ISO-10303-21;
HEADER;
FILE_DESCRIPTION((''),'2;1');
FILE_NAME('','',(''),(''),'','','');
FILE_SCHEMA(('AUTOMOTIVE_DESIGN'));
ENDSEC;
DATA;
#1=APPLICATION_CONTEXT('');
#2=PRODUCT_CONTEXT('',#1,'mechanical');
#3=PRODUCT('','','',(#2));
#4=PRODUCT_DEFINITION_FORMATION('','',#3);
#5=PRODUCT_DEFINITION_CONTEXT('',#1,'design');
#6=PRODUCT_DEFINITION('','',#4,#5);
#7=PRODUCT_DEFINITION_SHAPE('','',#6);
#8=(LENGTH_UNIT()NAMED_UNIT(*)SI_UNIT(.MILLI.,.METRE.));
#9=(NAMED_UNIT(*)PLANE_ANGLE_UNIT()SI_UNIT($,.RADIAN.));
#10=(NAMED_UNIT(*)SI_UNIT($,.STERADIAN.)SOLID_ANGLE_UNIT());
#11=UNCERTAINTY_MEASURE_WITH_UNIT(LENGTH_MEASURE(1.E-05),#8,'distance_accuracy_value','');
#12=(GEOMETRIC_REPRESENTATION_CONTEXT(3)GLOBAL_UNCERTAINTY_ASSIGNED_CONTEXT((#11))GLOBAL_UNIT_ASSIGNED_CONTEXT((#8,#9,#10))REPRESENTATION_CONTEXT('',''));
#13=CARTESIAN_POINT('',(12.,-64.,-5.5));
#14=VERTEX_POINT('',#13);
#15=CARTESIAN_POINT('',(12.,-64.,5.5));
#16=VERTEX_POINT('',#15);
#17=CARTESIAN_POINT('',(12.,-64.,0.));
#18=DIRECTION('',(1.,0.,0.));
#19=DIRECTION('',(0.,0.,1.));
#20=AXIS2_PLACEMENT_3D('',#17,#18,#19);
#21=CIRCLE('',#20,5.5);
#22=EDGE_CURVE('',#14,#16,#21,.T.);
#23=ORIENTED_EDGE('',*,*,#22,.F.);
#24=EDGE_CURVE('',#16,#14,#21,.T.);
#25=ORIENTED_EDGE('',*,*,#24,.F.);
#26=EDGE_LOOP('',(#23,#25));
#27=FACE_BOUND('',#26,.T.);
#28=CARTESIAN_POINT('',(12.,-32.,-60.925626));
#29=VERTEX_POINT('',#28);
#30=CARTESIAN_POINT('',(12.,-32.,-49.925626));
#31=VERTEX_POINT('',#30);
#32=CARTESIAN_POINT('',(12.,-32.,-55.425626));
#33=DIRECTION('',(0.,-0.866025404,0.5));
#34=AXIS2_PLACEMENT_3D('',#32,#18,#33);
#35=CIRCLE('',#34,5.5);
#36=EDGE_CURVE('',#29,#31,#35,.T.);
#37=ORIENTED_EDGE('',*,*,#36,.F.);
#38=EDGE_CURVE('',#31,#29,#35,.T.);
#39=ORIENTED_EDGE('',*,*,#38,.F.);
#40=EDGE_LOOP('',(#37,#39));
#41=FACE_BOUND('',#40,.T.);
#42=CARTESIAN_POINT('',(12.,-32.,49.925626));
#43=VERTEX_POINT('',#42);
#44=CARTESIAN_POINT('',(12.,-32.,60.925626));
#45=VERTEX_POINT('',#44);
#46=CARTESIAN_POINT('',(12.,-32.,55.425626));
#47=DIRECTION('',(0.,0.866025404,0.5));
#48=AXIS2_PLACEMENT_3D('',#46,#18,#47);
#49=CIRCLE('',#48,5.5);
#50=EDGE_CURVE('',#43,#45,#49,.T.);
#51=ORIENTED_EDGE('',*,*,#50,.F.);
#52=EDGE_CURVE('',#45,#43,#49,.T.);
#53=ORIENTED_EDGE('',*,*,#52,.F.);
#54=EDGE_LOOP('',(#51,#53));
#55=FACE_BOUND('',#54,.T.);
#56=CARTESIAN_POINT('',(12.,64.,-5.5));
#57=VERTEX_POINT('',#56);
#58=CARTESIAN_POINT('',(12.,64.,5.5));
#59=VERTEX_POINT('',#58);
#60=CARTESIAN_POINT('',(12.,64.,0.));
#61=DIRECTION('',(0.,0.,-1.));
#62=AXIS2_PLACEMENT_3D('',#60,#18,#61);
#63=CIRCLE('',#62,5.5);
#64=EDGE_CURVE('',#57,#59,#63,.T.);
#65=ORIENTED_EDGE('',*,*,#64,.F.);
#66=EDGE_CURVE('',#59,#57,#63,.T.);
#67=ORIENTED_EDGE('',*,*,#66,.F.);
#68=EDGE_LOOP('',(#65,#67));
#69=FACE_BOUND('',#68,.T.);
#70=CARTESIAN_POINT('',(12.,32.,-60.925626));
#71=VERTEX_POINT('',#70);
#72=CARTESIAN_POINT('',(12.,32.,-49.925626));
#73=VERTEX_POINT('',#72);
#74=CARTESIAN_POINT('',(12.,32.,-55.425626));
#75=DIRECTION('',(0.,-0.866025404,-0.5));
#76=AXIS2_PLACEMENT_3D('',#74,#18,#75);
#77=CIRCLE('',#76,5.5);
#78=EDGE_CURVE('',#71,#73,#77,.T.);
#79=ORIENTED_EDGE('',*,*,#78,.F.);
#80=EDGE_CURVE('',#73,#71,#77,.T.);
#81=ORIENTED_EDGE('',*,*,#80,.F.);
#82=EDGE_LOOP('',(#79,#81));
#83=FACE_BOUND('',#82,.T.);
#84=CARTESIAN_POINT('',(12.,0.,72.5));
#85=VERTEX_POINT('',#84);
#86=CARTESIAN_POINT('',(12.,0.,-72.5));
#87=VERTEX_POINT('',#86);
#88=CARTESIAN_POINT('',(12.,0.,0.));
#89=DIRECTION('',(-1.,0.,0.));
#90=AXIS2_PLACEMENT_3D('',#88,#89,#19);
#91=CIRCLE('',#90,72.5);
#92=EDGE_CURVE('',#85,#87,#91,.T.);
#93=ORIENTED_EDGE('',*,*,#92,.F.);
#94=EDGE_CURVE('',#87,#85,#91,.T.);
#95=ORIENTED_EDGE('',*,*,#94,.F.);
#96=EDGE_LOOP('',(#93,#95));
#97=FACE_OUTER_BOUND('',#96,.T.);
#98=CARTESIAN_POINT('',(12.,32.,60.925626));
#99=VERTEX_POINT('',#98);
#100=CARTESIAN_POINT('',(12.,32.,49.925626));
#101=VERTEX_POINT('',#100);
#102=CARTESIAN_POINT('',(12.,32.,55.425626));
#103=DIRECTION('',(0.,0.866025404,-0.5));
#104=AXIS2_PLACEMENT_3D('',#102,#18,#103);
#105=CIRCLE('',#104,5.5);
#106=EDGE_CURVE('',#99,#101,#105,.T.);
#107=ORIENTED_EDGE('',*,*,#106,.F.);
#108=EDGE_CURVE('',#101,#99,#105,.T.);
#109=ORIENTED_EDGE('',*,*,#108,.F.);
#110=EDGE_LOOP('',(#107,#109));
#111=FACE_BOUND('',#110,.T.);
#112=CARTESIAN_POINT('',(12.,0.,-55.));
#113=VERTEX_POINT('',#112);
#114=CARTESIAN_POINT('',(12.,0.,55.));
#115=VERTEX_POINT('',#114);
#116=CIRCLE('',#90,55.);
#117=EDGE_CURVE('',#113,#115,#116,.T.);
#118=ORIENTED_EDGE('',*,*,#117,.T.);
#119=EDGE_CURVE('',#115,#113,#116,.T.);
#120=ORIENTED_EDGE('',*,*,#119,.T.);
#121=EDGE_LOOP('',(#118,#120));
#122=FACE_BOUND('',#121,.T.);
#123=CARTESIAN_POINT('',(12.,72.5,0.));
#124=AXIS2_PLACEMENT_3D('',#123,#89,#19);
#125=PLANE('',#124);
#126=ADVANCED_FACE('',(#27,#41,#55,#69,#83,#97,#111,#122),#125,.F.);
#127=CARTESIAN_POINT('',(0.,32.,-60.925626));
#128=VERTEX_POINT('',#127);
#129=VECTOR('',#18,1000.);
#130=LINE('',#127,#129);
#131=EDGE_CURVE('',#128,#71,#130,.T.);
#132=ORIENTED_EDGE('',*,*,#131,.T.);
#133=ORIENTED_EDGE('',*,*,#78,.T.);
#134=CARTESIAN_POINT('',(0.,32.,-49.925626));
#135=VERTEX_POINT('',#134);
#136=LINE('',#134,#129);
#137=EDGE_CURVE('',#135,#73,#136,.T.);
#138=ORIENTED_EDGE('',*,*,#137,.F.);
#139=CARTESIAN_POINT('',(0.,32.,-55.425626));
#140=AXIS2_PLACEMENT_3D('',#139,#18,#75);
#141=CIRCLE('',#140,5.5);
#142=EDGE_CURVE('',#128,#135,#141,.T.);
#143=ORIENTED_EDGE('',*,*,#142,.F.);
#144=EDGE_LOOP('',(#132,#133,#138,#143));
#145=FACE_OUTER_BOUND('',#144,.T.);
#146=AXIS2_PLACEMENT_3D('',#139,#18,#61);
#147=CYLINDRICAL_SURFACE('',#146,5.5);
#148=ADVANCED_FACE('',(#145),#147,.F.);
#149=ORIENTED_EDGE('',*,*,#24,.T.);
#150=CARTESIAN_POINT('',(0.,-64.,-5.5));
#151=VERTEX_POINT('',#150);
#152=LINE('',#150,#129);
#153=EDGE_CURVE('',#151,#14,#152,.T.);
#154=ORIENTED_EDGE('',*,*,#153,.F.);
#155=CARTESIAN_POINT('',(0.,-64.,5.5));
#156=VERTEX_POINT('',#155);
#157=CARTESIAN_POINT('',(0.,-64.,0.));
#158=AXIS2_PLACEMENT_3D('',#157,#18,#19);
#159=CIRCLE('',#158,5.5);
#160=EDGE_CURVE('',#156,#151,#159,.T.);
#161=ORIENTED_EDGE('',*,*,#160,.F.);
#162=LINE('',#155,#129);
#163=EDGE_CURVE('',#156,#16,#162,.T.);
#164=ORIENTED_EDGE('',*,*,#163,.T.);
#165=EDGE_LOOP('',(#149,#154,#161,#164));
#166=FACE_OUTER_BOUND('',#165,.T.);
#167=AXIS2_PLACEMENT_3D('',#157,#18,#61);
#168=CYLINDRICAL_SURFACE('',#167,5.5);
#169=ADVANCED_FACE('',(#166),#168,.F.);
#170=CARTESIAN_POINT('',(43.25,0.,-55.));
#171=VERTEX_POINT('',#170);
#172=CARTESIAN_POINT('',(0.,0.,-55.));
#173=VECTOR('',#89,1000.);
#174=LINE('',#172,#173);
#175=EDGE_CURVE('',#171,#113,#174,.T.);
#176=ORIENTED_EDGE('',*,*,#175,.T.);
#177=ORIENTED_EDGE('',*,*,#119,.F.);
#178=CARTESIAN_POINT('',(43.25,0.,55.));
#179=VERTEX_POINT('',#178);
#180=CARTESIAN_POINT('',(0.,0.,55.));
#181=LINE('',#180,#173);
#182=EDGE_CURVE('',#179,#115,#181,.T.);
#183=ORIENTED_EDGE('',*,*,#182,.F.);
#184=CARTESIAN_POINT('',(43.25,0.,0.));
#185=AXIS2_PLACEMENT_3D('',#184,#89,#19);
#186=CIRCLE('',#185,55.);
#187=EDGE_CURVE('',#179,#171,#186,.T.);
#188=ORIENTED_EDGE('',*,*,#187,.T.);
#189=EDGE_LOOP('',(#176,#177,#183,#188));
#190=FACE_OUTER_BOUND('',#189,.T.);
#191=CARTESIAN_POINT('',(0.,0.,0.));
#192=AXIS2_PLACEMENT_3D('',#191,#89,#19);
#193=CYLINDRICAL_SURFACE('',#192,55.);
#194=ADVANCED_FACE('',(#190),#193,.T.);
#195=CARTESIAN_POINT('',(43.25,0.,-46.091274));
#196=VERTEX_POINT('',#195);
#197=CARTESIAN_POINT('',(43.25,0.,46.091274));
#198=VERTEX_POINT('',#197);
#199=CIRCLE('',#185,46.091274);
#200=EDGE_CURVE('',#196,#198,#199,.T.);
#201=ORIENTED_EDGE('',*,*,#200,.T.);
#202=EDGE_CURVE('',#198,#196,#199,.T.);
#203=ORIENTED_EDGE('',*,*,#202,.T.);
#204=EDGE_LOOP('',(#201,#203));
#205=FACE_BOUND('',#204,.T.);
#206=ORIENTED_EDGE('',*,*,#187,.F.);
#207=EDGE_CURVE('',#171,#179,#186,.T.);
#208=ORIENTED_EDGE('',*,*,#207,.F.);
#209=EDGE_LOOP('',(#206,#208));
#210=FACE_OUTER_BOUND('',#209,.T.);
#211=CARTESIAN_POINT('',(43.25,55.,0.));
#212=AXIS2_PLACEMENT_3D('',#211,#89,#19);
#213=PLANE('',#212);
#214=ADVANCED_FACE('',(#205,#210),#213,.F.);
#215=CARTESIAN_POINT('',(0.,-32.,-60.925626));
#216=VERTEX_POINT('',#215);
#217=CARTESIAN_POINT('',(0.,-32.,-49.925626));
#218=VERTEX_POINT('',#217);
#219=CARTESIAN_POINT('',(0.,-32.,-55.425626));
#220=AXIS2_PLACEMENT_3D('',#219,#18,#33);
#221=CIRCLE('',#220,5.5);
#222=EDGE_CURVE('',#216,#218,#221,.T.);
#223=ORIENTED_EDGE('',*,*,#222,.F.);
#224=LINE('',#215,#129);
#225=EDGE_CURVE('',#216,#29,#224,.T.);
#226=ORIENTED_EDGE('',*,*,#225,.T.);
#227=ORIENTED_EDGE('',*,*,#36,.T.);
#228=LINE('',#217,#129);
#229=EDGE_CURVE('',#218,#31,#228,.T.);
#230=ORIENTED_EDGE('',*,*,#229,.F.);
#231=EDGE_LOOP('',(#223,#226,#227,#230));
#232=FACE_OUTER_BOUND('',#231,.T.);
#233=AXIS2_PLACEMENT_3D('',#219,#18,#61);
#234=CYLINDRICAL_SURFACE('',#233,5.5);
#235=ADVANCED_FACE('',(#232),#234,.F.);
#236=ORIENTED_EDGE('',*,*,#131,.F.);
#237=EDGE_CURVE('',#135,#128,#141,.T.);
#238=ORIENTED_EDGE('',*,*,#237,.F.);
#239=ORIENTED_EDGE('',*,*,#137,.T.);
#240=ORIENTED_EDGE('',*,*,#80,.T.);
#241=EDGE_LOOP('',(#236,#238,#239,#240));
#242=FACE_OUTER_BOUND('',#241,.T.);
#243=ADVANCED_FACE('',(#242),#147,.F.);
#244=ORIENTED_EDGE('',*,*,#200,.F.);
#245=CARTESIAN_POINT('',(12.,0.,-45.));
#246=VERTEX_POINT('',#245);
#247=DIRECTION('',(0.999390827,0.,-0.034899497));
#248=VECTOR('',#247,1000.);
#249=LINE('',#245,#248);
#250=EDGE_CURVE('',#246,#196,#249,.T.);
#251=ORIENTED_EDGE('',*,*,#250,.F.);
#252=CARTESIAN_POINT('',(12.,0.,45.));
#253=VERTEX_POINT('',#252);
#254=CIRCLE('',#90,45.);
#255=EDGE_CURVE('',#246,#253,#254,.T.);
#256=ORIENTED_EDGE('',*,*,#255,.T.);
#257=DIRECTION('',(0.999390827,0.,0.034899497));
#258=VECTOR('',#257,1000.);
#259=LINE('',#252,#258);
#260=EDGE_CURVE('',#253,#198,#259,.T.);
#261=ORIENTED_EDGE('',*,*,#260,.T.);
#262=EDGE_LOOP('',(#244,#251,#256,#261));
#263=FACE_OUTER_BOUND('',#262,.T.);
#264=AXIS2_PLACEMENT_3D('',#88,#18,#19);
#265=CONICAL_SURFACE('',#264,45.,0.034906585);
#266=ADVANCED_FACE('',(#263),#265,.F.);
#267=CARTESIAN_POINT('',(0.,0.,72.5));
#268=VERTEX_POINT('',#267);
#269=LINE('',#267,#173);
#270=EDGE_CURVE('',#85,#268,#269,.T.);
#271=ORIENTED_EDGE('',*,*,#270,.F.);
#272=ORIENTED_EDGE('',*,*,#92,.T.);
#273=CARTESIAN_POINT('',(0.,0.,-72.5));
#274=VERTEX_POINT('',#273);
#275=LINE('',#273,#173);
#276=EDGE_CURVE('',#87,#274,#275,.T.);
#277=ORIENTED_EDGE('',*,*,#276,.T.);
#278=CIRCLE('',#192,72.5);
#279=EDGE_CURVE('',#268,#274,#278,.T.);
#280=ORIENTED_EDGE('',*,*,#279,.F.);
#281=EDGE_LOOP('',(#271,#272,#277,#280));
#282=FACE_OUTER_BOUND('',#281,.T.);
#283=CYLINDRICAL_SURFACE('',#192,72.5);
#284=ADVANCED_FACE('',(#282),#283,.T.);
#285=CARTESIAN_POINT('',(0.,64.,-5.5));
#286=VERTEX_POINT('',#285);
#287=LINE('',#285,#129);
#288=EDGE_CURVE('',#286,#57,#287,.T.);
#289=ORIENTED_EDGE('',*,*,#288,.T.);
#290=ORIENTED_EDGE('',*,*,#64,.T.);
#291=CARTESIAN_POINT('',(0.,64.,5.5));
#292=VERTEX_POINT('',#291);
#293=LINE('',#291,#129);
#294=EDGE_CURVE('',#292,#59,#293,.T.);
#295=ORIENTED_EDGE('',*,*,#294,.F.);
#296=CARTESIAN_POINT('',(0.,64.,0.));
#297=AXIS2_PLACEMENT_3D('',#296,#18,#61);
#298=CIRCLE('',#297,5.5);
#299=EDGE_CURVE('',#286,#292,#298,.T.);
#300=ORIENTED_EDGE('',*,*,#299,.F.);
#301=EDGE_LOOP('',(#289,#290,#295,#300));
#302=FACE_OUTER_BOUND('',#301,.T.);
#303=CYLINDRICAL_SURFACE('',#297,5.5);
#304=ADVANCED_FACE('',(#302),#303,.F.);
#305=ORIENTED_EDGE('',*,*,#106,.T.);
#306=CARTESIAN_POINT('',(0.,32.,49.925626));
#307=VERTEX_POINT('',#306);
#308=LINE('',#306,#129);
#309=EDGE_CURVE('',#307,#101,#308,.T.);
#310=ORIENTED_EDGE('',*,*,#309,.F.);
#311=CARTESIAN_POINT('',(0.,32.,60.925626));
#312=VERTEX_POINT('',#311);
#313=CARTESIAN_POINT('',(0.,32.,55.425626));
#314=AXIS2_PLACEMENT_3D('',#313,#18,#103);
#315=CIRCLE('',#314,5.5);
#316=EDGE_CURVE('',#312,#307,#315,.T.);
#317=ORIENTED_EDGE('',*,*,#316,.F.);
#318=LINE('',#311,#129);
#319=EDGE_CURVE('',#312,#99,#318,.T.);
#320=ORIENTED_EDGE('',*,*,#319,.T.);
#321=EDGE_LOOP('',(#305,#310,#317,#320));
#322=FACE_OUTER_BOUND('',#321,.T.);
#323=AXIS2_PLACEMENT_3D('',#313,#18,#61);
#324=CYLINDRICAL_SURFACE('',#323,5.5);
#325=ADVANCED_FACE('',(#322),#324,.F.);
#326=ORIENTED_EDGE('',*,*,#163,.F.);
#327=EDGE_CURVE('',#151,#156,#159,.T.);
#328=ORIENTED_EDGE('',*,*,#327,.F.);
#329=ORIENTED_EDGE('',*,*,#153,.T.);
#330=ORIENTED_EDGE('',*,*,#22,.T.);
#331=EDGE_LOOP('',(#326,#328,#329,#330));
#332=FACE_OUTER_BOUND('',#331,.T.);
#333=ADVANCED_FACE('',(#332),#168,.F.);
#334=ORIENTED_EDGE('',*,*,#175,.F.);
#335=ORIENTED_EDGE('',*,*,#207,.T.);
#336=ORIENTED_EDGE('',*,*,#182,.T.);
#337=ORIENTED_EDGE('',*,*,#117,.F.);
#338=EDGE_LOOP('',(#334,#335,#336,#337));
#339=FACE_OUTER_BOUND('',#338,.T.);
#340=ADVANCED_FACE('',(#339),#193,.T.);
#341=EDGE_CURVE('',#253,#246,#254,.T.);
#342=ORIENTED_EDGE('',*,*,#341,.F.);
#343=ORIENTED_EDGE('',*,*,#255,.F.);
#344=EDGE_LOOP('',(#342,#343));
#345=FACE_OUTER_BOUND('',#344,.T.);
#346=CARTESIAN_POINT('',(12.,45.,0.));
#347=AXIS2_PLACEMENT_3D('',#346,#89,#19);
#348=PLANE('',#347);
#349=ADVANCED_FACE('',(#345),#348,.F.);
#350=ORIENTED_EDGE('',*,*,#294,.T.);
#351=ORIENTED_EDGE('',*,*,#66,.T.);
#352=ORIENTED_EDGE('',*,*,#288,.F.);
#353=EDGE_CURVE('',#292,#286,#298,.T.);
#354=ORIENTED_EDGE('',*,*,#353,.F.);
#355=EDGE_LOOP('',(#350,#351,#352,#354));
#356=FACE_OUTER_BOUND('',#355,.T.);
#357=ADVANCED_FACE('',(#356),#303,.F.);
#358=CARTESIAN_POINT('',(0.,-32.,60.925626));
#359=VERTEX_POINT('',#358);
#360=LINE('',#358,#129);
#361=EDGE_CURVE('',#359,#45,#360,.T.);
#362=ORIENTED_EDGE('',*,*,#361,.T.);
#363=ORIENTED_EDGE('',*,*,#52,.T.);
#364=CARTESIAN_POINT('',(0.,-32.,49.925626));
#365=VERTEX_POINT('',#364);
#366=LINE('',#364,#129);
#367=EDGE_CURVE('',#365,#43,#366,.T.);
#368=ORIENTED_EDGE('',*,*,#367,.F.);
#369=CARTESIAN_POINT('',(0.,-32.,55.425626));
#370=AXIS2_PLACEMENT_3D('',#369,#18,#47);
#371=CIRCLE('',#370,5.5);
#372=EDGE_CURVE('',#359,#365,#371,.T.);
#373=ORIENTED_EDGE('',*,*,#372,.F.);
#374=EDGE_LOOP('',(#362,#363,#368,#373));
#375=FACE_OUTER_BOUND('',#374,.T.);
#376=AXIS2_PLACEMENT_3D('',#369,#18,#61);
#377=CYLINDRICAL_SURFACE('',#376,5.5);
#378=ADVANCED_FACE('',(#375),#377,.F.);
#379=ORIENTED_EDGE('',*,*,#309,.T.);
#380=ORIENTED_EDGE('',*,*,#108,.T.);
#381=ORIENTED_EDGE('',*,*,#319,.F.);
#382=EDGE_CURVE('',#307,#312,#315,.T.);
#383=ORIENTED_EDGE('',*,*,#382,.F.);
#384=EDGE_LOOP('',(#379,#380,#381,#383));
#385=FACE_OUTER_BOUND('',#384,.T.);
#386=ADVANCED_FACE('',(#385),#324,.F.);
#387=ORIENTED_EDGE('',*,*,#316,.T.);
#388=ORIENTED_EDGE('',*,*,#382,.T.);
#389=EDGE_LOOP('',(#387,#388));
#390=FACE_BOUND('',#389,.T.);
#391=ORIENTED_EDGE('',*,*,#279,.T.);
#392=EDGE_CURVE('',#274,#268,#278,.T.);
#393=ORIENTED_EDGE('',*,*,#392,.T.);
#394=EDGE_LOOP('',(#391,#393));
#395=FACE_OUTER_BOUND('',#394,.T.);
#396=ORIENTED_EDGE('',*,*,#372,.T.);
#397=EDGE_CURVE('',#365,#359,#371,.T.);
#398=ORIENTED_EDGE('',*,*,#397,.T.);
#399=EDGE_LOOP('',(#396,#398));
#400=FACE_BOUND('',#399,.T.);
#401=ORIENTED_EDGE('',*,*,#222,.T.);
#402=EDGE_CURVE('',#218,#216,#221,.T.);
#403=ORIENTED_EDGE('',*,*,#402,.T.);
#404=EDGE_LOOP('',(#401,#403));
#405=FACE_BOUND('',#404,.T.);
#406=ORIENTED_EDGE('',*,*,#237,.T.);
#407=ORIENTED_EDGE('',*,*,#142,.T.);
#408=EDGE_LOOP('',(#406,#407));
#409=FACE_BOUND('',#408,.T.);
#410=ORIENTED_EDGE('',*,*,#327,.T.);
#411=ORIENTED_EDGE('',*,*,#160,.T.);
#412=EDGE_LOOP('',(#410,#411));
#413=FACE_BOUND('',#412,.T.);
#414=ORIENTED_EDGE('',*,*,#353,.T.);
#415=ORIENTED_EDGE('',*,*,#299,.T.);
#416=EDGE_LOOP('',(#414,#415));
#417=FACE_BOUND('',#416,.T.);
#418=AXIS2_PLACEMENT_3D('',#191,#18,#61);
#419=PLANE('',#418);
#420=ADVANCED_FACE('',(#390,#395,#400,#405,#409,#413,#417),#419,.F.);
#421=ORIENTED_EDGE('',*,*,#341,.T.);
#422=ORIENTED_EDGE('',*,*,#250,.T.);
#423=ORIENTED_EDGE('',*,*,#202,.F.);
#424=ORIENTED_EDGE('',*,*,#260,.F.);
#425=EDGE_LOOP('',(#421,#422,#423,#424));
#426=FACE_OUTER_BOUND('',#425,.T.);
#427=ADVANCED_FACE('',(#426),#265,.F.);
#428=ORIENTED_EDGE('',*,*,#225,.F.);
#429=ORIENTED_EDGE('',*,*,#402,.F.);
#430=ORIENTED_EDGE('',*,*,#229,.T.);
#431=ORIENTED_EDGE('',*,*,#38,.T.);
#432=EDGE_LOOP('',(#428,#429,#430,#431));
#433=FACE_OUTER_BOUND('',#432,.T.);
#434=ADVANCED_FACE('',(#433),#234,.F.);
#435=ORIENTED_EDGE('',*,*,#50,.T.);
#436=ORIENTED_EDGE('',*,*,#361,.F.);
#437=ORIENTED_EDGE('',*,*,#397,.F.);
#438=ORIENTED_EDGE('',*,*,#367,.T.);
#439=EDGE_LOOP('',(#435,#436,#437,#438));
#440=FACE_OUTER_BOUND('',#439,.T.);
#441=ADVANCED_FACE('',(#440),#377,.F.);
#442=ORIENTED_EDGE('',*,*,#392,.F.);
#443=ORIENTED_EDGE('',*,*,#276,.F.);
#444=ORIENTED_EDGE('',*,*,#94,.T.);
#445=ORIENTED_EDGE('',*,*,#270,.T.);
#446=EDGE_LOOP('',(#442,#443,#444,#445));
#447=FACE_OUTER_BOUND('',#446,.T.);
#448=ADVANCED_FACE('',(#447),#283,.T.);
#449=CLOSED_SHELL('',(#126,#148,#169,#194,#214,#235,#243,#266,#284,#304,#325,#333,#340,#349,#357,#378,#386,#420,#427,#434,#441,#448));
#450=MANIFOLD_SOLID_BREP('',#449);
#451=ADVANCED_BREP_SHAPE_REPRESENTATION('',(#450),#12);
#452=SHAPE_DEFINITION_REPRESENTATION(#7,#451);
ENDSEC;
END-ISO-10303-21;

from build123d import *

# Parameters (mm, degrees)
SKETCH2_R          = 5.5
CUT_EXTRUDE1_DEPTH = 108.18704446
CIRPATTERN1_COUNT  = 6
DRAFT1_ANGLE       = 2


with BuildPart() as part:
    # Sketch1 → Revolve1 (revolve)
    with BuildSketch(Plane.XY, mode=Mode.PRIVATE) as revolve1_sk:
        Polygon((0, 0), (0, 72.5), (12, 72.5), (12, 55), (43.25, 55), (43.25, 45), (12, 45), (12, 0), align=None)
    revolve(revolve1_sk.sketch.rotate(Axis((0, 0, 0), (1, 0, 0)), 90), axis=Axis((0, 0, 0), (1, 0, 0)))

    # Sketch2 → Cut-Extrude1 (cut, through all)
    with BuildSketch(Plane(origin=(12, 0, 0), x_dir=(0, 0, -1), z_dir=(1, 0, 0))):
        with Locations((0, 64)):
            Circle(SKETCH2_R)
    cut_extrude1 = extrude(amount=-CUT_EXTRUDE1_DEPTH, mode=Mode.SUBTRACT)

    # CirPattern1: Cut-Extrude1 ×6 about axis
    cirpattern1_axis = Axis((0, 0, 0), (1, 0, 0))
    for i in range(1, CIRPATTERN1_COUNT):
        add(cut_extrude1.rotate(cirpattern1_axis, i * 360 / CIRPATTERN1_COUNT), mode=Mode.SUBTRACT)

    # Draft1
    draft1_faces = [part.faces().sort_by_distance(p)[0] for p in [
        (27.625, 0, -45),
    ]]
    draft(draft1_faces, Plane(origin=(12, 45, 0), x_dir=(0, 0, 1), z_dir=(1, 0, 0)), DRAFT1_ANGLE)


solid = part.part
